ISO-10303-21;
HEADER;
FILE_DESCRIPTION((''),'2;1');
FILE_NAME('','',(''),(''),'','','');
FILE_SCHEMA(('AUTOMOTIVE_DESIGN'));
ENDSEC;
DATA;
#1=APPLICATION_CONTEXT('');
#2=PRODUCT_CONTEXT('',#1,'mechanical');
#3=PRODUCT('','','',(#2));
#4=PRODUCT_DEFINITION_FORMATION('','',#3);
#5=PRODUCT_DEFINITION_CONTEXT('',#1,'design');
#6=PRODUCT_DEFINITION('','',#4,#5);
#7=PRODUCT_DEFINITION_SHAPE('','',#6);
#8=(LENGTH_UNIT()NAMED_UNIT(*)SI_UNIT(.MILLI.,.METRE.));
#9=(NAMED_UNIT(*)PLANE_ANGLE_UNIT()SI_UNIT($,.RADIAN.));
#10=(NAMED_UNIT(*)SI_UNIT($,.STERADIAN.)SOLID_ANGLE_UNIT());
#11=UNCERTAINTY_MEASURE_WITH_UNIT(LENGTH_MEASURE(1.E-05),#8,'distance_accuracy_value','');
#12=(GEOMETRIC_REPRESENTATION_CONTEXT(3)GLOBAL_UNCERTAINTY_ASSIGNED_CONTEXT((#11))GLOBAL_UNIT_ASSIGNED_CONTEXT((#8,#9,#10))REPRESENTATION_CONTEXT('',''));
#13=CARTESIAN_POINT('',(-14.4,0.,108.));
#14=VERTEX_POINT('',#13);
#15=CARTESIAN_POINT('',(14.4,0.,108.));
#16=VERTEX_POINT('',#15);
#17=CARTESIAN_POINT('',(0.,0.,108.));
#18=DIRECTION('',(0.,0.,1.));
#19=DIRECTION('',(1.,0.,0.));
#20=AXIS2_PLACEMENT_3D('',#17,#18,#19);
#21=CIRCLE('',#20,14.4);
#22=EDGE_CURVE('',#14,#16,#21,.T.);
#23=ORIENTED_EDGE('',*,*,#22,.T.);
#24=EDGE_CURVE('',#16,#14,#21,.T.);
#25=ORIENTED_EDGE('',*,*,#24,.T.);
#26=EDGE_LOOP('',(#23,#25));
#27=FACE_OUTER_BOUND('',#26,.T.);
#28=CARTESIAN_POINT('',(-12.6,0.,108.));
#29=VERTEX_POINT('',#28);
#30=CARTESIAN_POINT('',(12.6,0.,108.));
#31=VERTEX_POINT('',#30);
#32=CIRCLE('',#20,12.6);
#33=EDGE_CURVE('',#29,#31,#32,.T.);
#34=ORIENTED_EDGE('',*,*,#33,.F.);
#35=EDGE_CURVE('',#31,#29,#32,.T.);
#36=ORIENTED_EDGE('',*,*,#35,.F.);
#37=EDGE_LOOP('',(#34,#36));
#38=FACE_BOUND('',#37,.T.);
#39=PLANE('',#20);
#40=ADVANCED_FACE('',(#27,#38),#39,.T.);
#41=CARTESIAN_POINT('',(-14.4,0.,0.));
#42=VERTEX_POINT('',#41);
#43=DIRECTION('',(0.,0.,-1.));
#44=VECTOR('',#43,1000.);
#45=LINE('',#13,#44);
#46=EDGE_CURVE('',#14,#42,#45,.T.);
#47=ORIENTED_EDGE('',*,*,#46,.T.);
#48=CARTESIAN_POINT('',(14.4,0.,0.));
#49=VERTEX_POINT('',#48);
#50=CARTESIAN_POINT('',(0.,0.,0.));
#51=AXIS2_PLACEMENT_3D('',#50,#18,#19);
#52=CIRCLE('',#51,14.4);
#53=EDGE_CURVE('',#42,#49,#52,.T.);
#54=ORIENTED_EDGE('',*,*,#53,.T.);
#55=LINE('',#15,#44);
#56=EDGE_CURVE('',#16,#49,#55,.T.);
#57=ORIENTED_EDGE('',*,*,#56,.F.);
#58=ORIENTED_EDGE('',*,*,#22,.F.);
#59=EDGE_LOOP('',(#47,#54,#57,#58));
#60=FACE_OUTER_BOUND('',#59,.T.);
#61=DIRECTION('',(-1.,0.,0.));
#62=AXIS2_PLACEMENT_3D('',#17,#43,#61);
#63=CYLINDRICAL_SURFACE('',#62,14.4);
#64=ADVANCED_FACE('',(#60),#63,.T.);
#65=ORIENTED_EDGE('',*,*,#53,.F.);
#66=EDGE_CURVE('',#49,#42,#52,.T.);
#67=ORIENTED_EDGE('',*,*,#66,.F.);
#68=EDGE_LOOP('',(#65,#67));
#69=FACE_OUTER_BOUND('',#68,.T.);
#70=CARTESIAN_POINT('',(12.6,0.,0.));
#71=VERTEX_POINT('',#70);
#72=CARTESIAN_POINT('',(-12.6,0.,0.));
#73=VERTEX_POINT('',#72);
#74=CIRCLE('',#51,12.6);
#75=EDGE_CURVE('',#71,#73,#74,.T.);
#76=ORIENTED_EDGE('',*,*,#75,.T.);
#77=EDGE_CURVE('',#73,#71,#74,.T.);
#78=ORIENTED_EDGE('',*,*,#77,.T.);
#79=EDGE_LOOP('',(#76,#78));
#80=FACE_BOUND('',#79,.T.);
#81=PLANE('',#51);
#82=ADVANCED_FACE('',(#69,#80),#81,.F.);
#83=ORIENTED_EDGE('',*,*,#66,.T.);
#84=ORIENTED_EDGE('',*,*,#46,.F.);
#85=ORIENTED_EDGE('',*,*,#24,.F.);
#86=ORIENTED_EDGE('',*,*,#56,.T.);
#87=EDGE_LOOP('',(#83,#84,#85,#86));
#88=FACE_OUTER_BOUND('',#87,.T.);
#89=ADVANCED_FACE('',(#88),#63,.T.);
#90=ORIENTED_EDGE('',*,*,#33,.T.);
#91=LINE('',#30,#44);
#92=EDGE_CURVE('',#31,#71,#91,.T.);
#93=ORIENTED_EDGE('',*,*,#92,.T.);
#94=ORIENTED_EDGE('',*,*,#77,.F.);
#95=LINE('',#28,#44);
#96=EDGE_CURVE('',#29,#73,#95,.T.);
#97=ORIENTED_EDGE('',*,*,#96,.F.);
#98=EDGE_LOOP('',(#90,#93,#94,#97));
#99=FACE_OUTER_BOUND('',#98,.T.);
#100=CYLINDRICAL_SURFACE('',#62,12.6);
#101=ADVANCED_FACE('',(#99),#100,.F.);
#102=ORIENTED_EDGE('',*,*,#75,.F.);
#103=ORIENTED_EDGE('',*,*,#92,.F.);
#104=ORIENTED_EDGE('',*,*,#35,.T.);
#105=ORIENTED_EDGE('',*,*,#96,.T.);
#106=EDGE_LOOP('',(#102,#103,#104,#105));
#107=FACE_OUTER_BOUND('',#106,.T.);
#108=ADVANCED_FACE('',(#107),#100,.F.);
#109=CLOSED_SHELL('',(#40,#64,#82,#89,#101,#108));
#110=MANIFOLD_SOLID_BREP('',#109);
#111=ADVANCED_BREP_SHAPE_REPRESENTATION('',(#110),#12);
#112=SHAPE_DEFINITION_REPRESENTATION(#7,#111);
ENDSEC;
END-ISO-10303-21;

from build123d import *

# Parameters (mm, degrees)
SKETCH1_R           = 14.4
SKETCH1_R_2         = 12.6
BOSS_EXTRUDE1_DEPTH = 108


with BuildPart() as part:
    # Sketch1 → Boss-Extrude1 (new body)
    with BuildSketch(Plane.XY):
        Circle(SKETCH1_R)
        Circle(SKETCH1_R_2, mode=Mode.SUBTRACT)
    extrude(amount=BOSS_EXTRUDE1_DEPTH)


solid = part.part
